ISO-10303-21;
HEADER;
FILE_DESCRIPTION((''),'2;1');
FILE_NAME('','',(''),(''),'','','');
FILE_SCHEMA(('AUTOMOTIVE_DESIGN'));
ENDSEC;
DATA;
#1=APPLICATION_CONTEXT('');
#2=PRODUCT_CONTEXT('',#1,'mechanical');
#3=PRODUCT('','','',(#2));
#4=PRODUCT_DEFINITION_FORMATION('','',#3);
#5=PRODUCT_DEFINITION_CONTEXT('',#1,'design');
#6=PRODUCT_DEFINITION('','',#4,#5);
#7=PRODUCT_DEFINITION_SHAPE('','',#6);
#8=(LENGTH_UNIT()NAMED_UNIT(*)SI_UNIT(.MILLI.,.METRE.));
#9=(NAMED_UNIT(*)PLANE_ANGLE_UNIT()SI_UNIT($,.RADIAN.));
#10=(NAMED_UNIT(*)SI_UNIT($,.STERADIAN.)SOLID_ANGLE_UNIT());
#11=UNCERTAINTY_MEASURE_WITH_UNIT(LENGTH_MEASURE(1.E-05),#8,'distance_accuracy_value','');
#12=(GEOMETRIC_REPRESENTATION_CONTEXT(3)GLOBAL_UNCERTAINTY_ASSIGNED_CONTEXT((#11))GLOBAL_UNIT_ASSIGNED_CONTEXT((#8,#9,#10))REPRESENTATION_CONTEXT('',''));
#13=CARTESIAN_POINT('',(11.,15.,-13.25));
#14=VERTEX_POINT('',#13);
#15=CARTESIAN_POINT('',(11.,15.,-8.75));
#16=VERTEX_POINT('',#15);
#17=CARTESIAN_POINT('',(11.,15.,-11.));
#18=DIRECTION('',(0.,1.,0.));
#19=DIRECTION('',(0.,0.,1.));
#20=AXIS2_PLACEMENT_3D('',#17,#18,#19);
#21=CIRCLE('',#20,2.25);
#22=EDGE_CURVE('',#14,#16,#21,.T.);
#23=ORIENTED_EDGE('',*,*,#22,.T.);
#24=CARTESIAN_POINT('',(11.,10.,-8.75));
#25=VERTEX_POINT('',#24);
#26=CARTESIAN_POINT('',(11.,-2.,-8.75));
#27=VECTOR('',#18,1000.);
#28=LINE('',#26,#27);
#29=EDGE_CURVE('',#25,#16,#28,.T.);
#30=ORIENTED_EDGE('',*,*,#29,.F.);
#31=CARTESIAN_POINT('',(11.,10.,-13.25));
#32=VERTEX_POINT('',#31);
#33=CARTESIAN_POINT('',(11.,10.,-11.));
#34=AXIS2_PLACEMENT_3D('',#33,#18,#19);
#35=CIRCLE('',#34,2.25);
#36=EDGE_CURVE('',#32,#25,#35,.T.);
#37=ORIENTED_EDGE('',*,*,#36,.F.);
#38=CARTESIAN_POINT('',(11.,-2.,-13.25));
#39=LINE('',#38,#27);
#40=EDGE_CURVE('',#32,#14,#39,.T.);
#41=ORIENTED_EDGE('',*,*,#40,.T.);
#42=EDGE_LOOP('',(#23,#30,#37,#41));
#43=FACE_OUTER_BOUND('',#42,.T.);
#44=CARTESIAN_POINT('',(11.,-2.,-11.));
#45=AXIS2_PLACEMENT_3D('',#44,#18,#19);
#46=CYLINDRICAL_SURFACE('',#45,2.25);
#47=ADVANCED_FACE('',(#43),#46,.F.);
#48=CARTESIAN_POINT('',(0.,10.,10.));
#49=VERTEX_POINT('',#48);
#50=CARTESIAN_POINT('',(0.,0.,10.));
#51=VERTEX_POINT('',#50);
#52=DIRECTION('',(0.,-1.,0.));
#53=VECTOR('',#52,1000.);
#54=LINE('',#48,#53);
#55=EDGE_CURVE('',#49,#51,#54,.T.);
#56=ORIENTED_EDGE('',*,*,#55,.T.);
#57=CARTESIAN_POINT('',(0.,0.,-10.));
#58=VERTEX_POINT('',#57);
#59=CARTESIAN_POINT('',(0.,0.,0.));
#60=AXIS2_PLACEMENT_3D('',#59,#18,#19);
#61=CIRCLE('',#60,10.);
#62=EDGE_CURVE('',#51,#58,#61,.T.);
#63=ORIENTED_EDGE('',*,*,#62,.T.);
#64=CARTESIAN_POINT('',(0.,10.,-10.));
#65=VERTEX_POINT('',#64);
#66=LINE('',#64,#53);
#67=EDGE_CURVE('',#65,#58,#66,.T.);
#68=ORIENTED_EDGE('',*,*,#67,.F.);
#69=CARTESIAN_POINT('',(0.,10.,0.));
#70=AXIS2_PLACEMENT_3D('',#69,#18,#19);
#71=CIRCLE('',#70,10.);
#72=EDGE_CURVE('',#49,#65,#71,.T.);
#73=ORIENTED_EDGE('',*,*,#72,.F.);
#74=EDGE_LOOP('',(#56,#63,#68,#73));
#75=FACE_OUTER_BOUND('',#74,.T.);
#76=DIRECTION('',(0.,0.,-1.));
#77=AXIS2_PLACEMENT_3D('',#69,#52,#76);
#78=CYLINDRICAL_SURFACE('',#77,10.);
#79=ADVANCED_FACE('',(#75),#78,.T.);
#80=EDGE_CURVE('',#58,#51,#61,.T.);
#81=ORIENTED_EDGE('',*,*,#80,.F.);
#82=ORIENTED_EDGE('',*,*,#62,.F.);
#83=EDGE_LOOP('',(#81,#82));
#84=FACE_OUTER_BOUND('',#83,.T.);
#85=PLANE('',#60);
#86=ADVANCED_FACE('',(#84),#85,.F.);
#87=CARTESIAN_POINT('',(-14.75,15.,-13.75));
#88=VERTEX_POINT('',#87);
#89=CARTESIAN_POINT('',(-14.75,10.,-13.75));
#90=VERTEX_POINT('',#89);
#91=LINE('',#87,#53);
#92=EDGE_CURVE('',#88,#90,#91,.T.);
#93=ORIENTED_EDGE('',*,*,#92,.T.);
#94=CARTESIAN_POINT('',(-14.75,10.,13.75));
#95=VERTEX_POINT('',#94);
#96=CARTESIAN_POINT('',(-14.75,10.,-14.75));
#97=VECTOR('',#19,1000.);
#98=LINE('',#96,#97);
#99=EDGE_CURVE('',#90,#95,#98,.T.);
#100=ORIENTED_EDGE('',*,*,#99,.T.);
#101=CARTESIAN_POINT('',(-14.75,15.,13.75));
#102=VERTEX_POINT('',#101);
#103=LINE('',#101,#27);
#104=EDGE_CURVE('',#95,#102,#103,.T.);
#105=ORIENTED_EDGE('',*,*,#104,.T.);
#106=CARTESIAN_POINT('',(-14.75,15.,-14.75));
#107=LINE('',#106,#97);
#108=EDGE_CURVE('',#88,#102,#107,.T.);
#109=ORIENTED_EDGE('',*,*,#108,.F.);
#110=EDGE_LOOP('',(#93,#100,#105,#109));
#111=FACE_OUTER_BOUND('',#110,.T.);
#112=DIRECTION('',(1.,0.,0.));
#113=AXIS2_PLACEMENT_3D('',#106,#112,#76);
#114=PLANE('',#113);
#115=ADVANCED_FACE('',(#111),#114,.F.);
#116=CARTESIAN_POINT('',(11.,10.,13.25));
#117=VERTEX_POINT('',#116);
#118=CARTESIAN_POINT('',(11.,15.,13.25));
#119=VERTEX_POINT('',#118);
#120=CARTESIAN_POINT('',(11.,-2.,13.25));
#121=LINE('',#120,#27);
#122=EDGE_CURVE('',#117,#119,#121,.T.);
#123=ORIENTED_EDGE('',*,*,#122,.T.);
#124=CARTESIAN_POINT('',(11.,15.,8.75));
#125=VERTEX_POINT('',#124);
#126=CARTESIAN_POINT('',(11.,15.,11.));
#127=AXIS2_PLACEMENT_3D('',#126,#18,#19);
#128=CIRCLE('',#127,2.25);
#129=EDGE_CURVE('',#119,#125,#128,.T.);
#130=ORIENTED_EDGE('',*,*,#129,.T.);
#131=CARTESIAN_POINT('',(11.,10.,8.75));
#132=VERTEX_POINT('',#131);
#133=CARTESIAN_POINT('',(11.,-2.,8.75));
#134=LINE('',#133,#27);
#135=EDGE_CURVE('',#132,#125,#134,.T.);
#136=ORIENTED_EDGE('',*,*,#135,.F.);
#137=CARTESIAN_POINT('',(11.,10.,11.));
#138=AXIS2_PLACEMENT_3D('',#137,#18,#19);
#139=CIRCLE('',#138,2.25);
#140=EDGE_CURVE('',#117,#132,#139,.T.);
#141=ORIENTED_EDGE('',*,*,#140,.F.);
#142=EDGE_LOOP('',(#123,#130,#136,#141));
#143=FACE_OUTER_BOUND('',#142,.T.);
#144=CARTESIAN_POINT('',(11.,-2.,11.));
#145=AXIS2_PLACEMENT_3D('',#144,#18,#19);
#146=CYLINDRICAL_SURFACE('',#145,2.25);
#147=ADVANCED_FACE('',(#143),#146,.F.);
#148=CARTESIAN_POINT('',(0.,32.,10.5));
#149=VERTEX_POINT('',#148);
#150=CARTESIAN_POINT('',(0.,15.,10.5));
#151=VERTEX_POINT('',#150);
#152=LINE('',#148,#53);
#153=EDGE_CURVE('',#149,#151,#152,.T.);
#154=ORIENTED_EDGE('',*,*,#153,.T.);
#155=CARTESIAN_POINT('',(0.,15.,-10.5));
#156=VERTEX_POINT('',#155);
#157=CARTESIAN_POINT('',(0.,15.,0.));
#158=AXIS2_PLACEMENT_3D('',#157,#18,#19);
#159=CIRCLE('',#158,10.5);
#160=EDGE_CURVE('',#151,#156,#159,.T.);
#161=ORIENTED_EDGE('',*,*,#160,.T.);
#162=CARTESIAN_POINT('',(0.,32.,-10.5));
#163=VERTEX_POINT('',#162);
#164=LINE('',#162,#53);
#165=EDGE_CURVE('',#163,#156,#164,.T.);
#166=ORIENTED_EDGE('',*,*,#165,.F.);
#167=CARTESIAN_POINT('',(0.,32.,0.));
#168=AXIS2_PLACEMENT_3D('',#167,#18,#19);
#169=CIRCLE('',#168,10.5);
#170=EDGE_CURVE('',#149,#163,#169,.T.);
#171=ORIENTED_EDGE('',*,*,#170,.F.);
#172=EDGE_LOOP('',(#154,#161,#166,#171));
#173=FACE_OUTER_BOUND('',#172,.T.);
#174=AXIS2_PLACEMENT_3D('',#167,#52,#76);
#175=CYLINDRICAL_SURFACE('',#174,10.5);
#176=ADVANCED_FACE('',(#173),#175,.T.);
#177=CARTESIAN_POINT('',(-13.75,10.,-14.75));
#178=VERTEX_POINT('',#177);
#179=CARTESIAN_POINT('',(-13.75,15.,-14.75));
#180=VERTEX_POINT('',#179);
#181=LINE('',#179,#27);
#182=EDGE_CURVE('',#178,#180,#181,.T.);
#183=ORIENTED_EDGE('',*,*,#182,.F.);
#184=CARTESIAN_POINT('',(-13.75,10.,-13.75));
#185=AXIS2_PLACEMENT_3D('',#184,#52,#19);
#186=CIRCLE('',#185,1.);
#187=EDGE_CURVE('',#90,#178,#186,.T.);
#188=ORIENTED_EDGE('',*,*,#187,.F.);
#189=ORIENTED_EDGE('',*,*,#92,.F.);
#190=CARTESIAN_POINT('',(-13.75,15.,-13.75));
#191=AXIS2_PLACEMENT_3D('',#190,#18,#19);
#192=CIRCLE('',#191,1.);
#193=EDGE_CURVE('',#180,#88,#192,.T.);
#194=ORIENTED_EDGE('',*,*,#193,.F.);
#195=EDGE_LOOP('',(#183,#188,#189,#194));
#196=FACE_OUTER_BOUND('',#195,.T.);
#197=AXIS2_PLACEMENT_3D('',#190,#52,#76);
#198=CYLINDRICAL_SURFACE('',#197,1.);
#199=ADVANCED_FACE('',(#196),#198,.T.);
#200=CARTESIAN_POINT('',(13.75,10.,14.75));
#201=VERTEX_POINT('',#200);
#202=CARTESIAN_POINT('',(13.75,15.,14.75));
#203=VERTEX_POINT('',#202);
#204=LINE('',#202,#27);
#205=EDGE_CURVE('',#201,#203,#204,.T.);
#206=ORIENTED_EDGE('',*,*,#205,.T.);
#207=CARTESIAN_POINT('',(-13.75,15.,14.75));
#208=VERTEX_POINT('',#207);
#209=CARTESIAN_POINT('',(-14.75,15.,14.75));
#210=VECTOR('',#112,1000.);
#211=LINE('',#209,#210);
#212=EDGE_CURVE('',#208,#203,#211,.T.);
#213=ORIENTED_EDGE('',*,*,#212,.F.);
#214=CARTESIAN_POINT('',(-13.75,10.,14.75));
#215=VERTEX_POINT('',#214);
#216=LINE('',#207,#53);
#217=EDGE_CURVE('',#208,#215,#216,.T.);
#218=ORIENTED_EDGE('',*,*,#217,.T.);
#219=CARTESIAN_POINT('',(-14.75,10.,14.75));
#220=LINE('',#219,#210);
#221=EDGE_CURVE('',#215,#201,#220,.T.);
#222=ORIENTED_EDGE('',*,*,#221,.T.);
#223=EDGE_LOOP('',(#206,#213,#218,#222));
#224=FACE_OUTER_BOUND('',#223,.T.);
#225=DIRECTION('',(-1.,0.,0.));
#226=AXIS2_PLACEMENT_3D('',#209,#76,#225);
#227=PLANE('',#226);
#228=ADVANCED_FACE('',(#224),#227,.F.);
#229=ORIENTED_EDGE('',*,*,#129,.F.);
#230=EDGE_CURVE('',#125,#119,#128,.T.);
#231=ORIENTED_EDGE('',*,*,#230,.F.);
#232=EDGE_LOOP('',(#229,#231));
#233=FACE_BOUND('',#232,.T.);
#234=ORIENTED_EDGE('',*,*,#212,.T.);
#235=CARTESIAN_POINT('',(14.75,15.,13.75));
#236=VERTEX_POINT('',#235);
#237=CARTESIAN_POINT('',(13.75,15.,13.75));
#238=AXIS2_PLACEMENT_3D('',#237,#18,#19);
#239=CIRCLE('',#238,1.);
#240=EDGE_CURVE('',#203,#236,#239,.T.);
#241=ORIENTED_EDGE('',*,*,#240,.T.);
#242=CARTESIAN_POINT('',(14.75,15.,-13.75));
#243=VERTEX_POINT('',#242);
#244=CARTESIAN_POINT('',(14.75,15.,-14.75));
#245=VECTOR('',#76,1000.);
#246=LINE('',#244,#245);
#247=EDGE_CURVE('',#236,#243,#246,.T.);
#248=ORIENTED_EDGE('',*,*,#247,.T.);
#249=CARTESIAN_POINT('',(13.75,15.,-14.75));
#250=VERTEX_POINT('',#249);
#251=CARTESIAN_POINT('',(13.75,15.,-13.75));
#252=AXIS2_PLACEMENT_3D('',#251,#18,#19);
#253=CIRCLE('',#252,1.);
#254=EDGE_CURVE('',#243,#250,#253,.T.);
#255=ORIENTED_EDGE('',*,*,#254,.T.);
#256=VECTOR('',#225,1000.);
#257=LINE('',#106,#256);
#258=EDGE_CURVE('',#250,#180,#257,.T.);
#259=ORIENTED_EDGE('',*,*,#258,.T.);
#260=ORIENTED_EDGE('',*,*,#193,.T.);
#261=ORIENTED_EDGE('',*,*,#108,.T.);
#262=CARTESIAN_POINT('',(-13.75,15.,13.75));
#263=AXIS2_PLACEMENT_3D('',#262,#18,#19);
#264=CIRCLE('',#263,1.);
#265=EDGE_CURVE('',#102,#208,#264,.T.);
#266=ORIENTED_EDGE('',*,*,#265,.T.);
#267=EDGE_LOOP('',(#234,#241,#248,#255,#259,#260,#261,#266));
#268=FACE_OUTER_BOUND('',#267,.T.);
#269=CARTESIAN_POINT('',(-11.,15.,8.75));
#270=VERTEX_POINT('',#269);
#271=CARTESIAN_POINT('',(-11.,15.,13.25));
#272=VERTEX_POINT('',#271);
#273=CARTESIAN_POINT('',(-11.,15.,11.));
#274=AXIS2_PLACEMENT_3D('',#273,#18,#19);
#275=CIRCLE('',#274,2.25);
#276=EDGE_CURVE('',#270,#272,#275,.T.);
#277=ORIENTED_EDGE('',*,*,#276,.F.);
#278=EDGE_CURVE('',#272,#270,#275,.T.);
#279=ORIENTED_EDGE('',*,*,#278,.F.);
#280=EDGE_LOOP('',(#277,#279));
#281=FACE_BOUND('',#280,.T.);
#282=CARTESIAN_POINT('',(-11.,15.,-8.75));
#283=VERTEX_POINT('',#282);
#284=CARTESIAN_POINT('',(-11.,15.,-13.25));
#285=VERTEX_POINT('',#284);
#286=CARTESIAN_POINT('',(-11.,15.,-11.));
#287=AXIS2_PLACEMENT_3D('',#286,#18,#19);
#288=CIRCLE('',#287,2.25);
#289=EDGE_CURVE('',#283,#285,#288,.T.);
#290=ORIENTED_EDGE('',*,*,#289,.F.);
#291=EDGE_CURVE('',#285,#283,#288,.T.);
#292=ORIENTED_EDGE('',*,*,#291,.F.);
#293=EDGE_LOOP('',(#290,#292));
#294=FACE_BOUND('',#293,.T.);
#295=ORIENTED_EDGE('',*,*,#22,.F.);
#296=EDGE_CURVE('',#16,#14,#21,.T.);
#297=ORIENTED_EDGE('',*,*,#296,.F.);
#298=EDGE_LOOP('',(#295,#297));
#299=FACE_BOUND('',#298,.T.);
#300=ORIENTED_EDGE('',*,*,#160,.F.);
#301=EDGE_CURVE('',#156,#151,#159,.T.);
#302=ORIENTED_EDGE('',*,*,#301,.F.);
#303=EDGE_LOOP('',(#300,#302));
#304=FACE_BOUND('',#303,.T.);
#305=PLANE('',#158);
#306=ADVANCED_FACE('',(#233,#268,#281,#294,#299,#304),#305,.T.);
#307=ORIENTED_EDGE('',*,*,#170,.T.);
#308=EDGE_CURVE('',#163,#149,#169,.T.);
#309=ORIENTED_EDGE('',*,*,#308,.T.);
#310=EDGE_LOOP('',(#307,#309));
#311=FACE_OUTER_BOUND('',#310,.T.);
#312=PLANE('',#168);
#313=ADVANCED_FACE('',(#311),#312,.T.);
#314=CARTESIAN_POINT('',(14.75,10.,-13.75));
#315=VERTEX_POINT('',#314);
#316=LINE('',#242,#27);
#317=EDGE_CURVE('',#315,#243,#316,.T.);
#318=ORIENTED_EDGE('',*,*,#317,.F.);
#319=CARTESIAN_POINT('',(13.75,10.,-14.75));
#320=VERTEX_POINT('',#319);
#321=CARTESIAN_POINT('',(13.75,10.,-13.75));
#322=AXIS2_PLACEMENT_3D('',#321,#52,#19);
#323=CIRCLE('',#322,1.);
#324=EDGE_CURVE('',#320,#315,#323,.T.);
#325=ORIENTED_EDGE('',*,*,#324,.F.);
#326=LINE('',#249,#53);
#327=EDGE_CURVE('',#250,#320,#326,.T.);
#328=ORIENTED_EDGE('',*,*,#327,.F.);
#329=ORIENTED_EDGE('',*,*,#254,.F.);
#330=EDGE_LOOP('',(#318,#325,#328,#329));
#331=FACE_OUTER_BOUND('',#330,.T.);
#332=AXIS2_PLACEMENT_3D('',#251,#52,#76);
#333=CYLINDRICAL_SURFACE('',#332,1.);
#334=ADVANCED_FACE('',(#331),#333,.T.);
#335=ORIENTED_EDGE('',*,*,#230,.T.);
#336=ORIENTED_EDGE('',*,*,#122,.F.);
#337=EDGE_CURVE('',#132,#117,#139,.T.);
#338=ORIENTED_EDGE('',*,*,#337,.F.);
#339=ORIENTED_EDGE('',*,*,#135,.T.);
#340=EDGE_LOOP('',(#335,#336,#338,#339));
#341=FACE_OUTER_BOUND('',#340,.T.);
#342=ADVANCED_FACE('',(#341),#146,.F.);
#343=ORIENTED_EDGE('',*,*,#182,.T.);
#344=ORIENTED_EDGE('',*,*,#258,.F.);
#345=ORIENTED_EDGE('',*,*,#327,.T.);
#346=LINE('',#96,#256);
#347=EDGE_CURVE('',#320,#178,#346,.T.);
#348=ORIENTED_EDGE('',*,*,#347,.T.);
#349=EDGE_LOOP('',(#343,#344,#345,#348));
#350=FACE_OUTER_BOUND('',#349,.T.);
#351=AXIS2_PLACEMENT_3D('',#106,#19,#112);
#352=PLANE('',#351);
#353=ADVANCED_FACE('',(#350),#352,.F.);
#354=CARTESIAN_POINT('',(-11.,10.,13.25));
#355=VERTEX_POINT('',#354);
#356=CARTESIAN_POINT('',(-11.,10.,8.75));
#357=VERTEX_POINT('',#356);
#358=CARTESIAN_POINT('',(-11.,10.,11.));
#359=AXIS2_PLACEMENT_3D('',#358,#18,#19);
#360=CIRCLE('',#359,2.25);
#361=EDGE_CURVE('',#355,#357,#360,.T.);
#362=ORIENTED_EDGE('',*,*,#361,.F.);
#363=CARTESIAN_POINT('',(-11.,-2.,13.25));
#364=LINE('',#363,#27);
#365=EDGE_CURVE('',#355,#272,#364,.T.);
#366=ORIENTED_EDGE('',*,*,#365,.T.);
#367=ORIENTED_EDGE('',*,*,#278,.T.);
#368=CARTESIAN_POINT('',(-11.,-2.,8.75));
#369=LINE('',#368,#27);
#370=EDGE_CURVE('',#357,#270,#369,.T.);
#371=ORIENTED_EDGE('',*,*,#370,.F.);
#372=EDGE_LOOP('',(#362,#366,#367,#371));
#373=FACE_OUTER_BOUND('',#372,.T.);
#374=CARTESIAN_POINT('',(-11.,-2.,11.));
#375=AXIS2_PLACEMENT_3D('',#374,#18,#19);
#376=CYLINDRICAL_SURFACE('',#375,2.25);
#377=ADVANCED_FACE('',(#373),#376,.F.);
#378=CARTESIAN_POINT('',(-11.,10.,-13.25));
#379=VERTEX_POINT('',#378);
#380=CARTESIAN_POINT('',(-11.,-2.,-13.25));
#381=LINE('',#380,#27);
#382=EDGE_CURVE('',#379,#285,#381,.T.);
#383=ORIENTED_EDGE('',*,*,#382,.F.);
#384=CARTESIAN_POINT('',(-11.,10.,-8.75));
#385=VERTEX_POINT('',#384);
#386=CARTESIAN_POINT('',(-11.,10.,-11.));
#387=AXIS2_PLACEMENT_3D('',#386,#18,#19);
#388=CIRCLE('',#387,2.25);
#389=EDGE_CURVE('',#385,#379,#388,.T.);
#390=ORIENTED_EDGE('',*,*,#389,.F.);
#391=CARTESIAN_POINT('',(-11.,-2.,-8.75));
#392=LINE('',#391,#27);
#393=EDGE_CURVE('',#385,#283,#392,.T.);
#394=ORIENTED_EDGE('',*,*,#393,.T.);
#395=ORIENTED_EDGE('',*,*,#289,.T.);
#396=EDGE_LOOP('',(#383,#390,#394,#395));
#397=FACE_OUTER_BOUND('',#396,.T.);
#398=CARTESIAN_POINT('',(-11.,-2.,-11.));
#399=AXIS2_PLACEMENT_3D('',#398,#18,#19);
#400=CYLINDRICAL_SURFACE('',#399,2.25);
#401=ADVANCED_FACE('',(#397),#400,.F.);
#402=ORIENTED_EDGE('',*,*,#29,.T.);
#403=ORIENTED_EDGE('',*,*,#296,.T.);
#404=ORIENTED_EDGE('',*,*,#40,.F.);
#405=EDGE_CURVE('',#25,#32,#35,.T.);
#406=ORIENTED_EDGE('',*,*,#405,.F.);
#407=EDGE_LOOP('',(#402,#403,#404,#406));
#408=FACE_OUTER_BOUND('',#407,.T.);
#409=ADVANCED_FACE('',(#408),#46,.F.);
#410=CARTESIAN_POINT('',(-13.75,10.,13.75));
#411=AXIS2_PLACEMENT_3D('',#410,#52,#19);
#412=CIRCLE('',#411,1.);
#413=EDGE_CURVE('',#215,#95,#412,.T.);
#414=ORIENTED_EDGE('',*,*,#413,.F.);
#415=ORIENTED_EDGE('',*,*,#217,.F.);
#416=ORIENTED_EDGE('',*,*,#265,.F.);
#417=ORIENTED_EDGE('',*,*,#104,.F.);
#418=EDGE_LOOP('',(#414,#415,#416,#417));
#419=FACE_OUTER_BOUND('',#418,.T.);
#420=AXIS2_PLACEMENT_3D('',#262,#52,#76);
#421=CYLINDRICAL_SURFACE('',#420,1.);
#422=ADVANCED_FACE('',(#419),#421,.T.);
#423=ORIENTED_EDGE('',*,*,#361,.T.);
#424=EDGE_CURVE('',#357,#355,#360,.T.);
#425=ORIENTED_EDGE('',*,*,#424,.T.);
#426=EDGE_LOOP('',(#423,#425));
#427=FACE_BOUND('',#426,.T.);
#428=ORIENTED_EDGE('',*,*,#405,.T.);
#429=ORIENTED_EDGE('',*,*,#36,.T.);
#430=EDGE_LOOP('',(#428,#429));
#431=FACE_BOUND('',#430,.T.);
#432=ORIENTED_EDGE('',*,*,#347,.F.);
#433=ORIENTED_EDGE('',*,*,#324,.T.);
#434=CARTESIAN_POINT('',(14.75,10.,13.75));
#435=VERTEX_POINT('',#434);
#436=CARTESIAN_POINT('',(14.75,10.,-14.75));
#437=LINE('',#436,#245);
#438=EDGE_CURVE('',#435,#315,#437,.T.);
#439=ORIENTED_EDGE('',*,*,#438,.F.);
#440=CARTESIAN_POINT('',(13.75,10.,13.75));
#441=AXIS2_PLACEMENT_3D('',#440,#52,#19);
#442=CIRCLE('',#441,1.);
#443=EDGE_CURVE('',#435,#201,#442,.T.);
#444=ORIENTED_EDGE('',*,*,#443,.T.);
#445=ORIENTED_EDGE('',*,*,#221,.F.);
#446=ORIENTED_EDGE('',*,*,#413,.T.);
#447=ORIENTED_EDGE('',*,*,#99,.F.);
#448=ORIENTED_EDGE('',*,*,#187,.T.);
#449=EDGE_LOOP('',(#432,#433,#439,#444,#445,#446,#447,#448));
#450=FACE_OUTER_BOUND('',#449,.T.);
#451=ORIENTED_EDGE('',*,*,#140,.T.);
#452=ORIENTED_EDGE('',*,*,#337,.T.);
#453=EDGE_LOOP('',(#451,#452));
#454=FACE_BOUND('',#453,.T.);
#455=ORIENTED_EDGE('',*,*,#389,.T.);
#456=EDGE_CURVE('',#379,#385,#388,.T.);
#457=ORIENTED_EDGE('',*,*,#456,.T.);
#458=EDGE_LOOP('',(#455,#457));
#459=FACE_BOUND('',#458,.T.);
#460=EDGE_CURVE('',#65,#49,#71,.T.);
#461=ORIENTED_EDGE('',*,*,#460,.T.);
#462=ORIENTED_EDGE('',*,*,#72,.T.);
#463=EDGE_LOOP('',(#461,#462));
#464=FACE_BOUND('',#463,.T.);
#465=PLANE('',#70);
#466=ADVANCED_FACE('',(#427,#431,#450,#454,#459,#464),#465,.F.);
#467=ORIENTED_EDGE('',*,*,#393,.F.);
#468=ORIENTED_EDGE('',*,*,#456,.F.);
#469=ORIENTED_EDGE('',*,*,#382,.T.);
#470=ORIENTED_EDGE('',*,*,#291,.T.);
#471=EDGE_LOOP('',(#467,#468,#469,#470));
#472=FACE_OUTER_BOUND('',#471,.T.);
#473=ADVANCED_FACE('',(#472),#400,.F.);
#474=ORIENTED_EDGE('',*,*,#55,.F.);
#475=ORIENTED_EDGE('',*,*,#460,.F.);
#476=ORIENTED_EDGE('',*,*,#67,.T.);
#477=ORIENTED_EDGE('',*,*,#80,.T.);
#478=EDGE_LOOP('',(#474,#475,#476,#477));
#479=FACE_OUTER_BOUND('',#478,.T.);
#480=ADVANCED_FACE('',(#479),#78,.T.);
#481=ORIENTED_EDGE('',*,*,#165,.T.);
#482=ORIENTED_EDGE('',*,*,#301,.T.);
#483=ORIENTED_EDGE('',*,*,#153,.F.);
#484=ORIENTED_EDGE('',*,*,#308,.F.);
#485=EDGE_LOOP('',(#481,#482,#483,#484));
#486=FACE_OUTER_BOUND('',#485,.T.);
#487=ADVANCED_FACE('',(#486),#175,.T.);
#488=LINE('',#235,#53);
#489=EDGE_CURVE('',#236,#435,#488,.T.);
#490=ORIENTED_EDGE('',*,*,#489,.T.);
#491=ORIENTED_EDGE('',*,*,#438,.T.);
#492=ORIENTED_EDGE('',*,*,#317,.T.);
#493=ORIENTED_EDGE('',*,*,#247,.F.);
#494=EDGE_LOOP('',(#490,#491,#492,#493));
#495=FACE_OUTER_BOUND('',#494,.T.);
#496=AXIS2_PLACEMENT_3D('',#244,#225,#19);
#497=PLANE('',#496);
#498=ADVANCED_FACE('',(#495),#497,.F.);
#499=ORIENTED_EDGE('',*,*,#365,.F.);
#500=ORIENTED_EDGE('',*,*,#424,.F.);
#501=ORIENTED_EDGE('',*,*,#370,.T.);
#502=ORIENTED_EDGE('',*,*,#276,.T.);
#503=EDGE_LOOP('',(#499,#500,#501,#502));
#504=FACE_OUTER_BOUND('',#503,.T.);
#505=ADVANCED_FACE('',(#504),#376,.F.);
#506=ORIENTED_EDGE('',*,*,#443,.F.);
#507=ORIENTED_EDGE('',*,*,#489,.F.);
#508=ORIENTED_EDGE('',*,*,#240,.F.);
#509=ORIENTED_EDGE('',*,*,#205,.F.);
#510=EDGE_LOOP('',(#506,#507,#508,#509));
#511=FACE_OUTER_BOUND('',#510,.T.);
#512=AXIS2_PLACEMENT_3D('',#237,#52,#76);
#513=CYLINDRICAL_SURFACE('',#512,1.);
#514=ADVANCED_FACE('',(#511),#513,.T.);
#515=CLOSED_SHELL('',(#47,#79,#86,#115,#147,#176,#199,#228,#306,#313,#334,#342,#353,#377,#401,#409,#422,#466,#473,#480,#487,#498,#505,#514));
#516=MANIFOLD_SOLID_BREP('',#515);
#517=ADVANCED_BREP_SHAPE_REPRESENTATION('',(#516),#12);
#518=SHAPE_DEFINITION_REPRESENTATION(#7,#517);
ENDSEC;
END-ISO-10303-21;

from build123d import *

# Parameters (mm, degrees)
SKETCH_1_R          = 10
EXTRUDE_1_DEPTH     = 10
SKETCH_2_W          = 29.5
SKETCH_2_H          = 29.5
EXTRUDE_2_DEPTH     = 5
SKETCH_3_R          = 10.5
EXTRUDE_3_DEPTH     = 17
SKETCH_4_R          = 2.25
CUT_EXTRUDE_1_DEPTH = 17
FILLET_1_R          = 1


with BuildPart() as part:
    # 草图1 → 凸台-拉伸1 (new body)
    with BuildSketch(Plane(origin=(0, 0, 0), x_dir=(1, 0, 0), z_dir=(0, 1, 0))):
        with Locations(Location((0, 0, 0), (0, 0, 270))):
            Circle(SKETCH_1_R)
    extrude(amount=EXTRUDE_1_DEPTH)

    # 草图2 → 凸台-拉伸2 (add)
    with BuildSketch(Plane(origin=(0, 10, 0), x_dir=(1, 0, 0), z_dir=(0, 1, 0))):
        Rectangle(SKETCH_2_W, SKETCH_2_H)
    extrude(amount=EXTRUDE_2_DEPTH)

    # 草图3 → 凸台-拉伸3 (add)
    with BuildSketch(Plane(origin=(0, 15, 0), x_dir=(1, 0, 0), z_dir=(0, 1, 0))):
        with Locations(Location((0, 0, 0), (0, 0, 270))):
            Circle(SKETCH_3_R)
    extrude(amount=EXTRUDE_3_DEPTH)

    # 草图4 → 切除-拉伸1 (cut)
    with BuildSketch(Plane(origin=(0, 15, 0), x_dir=(1, 0, 0), z_dir=(0, 1, 0))):
        with Locations(Location((11, 11, 0), (0, 0, 270))):
            Circle(SKETCH_4_R)
        with Locations(Location((-11, 11, 0), (0, 0, 270))):
            Circle(SKETCH_4_R)
        with Locations(Location((-11, -11, 0), (0, 0, 270))):
            Circle(SKETCH_4_R)
        with Locations(Location((11, -11, 0), (0, 0, 270))):
            Circle(SKETCH_4_R)
    extrude(amount=-CUT_EXTRUDE_1_DEPTH, mode=Mode.SUBTRACT)

    # 圆角1
    fillet_1_edges = [part.edges().sort_by_distance(p)[0] for p in [
        (14.75, 12.5, 14.75),
        (14.75, 12.5, -14.75),
        (-14.75, 12.5, -14.75),
        (-14.75, 12.5, 14.75),
    ]]
    fillet(fillet_1_edges, radius=FILLET_1_R)


solid = part.part
